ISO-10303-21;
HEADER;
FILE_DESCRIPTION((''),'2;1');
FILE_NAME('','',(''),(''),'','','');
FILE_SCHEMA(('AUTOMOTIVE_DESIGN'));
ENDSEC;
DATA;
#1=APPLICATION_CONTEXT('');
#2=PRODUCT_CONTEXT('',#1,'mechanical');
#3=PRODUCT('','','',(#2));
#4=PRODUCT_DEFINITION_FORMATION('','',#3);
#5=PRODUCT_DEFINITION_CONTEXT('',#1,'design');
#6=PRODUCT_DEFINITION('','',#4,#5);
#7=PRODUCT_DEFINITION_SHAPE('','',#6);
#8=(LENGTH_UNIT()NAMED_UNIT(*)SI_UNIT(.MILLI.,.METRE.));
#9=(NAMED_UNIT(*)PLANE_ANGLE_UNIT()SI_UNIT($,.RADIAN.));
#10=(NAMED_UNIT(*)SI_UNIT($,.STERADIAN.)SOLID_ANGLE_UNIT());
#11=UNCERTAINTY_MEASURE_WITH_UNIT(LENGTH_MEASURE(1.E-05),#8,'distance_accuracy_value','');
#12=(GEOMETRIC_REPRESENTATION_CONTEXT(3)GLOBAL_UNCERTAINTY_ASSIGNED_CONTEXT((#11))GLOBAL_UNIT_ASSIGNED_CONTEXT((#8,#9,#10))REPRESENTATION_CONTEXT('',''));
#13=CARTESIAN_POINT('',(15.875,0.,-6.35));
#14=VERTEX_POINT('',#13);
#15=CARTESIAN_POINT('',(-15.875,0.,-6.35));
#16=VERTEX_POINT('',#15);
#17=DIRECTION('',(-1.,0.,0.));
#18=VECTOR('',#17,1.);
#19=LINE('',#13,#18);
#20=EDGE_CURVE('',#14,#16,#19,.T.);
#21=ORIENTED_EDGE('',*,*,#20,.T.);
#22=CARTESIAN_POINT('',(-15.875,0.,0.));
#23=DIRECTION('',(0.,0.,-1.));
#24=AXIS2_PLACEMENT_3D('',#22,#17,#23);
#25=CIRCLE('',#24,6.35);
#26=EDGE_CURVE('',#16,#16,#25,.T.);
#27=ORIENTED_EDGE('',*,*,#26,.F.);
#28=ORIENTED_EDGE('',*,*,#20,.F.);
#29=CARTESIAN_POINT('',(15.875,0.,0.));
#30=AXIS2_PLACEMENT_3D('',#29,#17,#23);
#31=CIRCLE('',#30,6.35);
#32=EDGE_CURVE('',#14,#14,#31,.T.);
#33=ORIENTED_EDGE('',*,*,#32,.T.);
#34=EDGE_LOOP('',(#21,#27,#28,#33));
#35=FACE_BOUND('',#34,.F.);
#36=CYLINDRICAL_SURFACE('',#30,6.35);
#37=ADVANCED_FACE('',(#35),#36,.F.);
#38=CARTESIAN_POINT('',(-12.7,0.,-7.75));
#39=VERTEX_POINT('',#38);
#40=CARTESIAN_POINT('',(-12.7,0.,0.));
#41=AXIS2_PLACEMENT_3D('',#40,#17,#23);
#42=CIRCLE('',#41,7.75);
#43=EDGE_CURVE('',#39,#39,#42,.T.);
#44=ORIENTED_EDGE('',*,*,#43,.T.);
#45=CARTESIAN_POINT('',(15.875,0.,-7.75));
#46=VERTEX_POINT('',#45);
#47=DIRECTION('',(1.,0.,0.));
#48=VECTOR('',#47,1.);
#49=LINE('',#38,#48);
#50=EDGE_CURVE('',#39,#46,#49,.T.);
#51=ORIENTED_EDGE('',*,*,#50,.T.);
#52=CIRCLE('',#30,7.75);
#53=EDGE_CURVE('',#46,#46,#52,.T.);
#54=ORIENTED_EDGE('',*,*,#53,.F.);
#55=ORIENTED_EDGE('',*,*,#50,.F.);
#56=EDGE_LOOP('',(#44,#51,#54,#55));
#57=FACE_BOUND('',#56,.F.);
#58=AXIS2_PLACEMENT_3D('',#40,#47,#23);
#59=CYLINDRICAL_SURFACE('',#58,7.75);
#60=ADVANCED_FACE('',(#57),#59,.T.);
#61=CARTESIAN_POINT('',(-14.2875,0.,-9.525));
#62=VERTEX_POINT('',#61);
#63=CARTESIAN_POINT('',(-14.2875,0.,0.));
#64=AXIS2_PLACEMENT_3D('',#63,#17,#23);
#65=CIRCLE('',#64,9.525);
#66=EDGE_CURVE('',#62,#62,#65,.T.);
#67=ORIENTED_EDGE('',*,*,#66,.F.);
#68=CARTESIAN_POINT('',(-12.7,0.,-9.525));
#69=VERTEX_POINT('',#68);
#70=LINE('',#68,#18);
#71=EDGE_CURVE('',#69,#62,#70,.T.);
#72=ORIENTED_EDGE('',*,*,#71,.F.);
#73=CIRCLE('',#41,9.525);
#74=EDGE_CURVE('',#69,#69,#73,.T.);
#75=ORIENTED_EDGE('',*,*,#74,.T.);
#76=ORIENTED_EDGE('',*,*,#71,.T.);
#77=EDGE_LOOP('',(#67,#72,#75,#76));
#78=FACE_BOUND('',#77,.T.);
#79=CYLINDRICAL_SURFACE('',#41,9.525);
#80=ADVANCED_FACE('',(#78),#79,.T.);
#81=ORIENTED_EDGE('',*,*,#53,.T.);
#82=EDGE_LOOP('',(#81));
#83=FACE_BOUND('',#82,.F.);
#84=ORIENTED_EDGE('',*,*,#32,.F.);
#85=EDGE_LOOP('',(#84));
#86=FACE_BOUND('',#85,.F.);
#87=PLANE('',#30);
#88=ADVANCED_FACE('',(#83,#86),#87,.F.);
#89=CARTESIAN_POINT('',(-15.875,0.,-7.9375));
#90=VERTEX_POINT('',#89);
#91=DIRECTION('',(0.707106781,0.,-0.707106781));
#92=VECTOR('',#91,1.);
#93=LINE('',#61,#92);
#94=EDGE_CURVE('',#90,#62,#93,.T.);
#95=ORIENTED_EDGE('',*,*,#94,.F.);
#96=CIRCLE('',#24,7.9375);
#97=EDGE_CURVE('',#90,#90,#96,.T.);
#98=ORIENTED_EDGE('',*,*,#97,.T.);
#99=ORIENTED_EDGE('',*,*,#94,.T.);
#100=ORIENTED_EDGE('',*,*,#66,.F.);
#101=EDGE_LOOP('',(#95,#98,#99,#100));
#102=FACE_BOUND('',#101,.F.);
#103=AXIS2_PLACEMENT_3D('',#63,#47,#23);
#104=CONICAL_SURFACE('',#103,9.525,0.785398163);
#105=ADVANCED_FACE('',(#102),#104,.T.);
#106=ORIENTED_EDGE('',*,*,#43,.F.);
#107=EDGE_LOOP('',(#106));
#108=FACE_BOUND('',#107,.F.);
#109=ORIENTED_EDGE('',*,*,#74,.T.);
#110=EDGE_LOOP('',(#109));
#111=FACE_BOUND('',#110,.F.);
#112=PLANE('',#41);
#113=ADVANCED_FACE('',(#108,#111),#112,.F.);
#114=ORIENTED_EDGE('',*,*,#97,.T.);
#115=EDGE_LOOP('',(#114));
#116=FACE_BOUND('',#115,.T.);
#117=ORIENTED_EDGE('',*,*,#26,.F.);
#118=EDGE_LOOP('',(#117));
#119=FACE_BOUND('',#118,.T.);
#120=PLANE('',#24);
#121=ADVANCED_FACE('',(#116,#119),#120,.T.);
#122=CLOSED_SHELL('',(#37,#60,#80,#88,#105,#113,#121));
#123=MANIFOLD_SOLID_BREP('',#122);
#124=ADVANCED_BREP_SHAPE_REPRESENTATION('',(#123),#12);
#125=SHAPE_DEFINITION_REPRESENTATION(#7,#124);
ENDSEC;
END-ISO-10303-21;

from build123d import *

# Parameters (mm, degrees)
EDGE_CHAMFER_0_0625IN_X_45DEG_SIZE = 1.5875


with BuildPart() as part:
    # Bushing Profile Sketch → Flanged Bushing Revolve (revolve)
    with BuildSketch(Plane.XY, mode=Mode.PRIVATE) as flanged_bushing_revolve_sk:
        Polygon((15.875, 6.35), (-15.875, 6.35), (-15.875, 8.89), (-15.875, 9.525), (-14.2875, 9.525), (-12.7, 9.525), (-12.7, 7.75), (15.875, 7.75), align=None)
    revolve(flanged_bushing_revolve_sk.sketch.rotate(Axis((40.781111111, 0, 0), (-1, 0, 0)), 90), axis=Axis((40.781111111, 0, 0), (-1, 0, 0)))

    # Edge Chamfer 0.0625in x 45deg
    edge_chamfer_0_0625in_x_45deg_edges = [part.edges().sort_by_distance(p)[0] for p in [
        (-15.875, 0, 9.525),
    ]]
    chamfer(edge_chamfer_0_0625in_x_45deg_edges, length=EDGE_CHAMFER_0_0625IN_X_45DEG_SIZE)


solid = part.part
